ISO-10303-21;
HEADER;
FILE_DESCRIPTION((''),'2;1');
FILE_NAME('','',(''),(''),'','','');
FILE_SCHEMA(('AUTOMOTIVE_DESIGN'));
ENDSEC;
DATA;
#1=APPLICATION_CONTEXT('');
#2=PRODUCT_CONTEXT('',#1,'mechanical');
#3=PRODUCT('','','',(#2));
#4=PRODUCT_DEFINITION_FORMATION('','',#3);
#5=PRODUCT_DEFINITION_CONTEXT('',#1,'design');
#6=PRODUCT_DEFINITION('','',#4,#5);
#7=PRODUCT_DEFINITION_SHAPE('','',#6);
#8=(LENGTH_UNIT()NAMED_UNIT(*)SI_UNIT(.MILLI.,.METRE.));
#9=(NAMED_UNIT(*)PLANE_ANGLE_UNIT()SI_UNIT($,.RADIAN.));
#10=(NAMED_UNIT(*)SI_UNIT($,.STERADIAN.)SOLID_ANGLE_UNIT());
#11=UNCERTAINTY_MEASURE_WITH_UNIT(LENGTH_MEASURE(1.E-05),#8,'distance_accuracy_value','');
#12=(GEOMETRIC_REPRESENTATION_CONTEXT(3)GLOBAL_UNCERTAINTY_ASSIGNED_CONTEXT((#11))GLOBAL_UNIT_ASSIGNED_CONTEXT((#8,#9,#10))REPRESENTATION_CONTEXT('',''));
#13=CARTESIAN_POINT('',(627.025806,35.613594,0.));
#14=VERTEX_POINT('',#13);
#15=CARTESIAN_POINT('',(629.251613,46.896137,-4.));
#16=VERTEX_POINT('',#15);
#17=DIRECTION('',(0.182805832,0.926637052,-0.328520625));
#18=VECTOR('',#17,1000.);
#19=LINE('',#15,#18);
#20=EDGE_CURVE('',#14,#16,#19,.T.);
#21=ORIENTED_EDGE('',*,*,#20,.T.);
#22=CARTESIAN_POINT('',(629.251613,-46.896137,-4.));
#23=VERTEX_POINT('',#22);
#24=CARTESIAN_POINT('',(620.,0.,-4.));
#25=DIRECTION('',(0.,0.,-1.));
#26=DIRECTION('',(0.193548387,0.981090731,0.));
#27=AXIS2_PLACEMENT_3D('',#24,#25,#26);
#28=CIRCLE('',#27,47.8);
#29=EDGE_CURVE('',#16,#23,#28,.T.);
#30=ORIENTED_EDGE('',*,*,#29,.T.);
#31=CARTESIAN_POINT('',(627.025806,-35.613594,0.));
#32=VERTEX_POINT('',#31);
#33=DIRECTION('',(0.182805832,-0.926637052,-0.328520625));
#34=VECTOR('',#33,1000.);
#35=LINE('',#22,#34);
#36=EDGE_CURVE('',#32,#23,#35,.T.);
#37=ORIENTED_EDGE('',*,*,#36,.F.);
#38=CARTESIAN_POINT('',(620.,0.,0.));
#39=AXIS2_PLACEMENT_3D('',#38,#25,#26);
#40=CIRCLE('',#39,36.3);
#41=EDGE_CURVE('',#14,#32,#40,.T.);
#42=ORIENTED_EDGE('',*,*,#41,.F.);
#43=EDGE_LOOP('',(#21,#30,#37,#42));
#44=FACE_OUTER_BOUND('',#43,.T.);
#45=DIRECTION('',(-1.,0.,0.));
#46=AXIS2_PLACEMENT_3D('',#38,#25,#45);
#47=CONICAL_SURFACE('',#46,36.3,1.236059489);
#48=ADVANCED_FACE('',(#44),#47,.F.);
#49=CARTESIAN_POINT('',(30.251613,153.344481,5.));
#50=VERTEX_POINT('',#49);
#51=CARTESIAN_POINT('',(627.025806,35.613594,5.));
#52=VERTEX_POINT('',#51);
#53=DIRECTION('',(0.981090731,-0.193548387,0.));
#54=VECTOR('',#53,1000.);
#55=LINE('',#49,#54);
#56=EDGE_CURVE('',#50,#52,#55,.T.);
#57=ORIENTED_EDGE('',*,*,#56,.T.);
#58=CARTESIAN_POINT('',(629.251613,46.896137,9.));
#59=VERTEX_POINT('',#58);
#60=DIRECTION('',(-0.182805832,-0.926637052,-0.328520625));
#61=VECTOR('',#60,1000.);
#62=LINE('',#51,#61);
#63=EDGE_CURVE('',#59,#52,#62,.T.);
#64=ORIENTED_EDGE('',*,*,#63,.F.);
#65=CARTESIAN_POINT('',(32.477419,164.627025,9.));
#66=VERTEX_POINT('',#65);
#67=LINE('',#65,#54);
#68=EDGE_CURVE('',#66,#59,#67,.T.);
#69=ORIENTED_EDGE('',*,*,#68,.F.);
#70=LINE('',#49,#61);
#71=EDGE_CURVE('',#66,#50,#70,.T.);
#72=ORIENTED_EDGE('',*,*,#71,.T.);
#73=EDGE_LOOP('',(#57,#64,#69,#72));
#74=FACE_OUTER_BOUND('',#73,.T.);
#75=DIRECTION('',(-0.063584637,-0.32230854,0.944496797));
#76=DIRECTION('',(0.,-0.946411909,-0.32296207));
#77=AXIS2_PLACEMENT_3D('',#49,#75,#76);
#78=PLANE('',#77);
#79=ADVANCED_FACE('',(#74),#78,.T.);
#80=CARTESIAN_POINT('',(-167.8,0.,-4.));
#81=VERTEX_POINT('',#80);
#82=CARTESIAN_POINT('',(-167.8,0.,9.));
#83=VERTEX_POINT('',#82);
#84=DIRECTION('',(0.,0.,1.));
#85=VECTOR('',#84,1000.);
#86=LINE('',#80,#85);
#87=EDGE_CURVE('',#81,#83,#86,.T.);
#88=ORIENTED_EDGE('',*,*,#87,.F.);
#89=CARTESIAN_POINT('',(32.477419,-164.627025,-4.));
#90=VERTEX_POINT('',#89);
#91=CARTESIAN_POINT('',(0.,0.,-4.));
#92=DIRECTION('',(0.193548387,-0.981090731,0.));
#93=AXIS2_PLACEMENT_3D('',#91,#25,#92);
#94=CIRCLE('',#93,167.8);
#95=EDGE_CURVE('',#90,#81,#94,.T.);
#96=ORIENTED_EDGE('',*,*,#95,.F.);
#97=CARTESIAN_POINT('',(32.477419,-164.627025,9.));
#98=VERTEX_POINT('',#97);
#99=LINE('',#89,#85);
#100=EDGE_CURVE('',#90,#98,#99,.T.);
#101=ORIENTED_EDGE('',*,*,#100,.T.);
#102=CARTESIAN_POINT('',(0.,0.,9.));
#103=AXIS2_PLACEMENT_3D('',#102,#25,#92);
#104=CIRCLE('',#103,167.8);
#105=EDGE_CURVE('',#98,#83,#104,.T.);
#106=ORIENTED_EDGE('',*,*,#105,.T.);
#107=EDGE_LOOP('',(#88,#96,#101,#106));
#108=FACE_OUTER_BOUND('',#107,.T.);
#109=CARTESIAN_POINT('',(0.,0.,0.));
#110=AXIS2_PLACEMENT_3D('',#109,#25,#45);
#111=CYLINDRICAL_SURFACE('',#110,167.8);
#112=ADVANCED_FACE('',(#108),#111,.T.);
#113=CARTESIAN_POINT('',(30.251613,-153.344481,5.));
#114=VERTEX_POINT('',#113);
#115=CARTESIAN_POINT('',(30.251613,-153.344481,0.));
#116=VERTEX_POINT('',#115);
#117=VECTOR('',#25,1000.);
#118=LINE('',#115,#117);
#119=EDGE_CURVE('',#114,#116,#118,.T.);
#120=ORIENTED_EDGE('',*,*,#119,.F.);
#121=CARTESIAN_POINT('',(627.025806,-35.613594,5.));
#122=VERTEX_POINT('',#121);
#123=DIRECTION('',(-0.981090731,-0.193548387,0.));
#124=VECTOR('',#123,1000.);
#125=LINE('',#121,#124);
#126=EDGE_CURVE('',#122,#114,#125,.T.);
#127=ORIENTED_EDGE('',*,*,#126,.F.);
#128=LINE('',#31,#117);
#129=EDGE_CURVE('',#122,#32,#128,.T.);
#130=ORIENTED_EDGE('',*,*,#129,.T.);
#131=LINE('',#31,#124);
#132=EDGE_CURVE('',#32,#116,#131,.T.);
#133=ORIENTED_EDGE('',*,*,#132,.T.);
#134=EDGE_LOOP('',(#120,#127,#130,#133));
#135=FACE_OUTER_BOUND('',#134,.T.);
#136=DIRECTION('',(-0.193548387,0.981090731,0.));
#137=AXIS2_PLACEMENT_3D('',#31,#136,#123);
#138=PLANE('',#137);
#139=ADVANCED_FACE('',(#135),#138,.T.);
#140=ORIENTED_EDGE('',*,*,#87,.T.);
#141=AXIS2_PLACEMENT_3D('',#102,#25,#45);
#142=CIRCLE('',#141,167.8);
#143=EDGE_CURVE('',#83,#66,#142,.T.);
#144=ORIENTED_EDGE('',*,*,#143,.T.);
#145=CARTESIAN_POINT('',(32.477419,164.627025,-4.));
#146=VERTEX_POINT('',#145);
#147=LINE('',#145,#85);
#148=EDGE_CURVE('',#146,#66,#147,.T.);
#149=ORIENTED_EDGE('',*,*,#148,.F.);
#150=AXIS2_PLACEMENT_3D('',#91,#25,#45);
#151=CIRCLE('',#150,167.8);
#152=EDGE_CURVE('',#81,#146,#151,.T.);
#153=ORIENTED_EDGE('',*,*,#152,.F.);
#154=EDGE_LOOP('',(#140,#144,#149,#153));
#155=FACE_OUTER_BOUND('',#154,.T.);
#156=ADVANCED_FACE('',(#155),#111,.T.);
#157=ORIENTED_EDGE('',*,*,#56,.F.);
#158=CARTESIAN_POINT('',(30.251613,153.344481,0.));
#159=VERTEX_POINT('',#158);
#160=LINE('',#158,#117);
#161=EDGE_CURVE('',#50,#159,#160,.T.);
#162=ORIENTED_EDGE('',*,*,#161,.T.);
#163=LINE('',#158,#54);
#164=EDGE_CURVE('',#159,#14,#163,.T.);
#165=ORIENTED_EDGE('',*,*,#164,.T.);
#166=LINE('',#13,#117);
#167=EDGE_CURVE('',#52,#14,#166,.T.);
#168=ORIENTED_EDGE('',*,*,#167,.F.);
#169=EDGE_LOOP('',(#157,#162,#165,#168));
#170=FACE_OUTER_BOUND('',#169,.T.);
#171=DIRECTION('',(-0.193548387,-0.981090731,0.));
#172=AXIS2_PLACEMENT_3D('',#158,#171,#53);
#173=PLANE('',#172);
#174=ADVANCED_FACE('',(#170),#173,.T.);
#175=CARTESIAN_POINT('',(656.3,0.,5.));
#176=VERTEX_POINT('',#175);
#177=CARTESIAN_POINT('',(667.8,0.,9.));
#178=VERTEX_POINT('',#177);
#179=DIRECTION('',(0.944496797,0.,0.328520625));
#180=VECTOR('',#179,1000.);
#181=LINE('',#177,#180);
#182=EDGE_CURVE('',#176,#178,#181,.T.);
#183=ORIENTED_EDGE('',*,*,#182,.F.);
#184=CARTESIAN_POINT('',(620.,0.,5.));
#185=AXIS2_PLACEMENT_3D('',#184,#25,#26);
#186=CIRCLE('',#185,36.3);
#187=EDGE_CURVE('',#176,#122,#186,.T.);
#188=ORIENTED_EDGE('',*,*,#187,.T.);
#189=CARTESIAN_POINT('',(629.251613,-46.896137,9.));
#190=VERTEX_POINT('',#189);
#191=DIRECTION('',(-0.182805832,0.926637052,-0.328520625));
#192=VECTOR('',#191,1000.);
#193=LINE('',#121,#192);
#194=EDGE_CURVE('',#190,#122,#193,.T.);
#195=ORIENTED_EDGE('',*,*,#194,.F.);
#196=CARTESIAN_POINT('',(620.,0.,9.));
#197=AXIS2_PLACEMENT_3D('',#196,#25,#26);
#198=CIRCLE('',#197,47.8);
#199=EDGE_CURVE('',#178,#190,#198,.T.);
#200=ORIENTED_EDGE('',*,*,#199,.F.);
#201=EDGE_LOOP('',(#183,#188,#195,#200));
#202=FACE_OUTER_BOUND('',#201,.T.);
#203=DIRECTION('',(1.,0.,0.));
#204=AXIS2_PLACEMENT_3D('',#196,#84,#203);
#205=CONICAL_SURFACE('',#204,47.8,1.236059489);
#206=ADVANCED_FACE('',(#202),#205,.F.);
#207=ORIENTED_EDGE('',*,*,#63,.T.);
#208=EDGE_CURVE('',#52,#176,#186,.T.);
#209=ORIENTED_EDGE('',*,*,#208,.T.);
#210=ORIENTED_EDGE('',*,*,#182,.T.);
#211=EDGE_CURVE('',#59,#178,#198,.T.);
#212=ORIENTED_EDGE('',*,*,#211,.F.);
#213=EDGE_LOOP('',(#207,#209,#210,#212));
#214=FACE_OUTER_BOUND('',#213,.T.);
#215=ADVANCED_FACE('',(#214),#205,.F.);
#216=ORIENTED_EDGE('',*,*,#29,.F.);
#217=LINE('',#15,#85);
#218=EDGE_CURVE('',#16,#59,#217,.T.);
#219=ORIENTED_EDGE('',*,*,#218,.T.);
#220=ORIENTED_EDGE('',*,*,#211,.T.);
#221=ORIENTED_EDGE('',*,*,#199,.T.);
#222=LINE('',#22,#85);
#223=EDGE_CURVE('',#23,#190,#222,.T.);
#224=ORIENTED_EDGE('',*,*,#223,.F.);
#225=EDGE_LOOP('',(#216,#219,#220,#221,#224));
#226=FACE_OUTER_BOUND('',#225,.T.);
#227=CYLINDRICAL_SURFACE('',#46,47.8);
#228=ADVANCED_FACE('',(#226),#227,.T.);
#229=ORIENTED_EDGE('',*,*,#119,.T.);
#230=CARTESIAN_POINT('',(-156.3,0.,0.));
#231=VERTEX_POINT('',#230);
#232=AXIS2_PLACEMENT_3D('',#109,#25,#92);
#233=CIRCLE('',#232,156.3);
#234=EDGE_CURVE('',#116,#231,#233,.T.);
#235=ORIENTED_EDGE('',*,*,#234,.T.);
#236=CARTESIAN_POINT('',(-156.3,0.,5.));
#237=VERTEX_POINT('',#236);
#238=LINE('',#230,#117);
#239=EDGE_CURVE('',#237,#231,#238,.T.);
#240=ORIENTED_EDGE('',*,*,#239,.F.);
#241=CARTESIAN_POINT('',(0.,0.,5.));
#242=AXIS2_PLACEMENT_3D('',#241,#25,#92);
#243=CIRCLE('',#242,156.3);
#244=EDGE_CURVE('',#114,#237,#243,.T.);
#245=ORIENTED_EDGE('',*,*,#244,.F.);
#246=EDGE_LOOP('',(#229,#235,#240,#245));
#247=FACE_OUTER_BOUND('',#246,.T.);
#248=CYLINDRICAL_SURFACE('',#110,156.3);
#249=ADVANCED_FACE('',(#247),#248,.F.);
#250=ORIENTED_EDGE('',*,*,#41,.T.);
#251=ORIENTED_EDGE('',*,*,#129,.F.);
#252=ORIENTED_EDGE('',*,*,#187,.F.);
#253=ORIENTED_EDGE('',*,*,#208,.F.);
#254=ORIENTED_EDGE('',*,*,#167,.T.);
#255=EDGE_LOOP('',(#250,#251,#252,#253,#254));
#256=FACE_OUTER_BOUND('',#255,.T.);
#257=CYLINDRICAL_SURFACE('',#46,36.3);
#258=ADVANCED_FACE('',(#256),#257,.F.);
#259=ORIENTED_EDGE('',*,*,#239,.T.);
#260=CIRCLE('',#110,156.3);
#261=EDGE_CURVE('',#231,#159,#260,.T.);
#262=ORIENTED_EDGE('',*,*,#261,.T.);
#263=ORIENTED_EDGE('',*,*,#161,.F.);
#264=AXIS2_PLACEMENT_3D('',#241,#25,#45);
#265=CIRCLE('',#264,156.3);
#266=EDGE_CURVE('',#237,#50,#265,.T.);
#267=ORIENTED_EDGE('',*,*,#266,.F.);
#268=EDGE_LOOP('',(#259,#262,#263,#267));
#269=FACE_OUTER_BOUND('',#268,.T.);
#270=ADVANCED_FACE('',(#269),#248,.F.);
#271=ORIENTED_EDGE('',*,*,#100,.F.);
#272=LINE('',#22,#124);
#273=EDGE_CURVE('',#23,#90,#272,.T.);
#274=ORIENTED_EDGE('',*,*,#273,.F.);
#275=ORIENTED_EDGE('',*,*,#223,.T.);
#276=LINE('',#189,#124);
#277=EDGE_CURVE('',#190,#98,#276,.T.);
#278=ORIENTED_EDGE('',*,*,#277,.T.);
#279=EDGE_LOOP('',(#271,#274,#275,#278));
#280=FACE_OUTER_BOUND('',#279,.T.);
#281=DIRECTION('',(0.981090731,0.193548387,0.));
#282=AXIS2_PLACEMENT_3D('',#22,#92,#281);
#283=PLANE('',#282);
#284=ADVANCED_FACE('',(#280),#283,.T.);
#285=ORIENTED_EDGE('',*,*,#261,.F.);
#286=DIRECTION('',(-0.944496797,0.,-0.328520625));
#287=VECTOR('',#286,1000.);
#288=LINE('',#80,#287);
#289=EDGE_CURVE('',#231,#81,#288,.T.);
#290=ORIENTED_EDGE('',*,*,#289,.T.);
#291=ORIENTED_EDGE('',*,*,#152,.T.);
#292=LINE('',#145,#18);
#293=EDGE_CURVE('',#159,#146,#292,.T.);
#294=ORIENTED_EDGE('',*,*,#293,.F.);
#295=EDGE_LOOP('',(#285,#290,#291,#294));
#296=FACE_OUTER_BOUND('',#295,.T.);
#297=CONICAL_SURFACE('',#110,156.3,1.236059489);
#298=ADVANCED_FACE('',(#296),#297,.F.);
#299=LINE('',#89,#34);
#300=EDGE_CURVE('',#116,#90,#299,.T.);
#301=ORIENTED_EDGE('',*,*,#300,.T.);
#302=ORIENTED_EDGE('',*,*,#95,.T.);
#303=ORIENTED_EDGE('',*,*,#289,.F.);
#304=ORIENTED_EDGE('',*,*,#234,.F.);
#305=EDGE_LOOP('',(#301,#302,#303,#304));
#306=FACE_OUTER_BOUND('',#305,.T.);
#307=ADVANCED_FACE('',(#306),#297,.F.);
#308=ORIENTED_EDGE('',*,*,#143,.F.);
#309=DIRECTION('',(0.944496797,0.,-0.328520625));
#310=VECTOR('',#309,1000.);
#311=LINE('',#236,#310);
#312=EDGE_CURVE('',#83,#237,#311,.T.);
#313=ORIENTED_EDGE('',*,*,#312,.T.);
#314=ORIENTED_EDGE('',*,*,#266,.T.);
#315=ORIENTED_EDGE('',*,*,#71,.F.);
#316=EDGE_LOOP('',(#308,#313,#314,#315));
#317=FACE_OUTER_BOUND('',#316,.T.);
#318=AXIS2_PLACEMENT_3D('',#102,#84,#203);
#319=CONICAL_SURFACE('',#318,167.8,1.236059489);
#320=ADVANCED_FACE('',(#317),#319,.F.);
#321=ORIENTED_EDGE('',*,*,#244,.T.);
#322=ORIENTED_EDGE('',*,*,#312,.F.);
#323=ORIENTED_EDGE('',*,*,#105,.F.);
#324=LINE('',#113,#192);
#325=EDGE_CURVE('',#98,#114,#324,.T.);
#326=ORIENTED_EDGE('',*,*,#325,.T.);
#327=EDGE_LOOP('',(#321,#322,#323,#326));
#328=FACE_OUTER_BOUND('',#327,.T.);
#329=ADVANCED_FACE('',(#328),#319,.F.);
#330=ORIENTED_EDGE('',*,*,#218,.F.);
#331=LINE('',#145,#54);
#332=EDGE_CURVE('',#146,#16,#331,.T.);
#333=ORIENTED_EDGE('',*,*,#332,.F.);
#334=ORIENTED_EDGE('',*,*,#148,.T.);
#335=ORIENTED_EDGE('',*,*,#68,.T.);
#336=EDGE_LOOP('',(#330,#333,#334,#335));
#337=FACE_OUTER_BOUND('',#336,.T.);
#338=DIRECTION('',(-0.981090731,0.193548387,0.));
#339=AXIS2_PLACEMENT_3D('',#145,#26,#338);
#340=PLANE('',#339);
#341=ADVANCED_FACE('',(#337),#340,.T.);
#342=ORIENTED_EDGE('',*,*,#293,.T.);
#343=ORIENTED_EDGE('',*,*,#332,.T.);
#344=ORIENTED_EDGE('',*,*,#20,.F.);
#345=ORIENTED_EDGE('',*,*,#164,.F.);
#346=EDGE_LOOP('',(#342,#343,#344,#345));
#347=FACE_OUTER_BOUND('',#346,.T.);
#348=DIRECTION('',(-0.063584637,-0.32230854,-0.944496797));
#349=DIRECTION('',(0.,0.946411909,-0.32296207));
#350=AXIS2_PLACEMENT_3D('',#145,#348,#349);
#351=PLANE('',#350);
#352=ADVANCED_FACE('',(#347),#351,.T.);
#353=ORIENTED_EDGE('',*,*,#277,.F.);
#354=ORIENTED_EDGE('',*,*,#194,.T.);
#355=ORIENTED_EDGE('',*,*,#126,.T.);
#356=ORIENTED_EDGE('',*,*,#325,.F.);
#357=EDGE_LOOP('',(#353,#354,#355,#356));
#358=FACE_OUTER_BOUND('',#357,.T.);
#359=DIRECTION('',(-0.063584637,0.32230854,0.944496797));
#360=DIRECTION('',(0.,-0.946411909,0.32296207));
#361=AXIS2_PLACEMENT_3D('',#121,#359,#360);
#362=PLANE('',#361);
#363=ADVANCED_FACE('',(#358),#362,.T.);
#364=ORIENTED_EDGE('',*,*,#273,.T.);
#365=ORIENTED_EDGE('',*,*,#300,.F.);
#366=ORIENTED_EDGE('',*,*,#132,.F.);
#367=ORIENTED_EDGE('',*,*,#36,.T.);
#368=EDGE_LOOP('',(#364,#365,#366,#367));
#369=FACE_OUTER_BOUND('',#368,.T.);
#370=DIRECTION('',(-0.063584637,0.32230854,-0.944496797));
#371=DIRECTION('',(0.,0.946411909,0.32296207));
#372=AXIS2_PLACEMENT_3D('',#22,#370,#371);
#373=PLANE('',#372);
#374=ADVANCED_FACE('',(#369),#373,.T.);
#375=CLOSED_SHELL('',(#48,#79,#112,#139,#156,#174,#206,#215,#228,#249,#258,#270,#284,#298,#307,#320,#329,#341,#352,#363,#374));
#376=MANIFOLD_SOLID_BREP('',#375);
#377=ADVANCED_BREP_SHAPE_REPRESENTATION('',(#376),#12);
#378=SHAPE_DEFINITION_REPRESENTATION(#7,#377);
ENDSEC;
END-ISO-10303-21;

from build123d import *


with BuildPart() as part:
    # Sweep1: sweep along a path in Sketch1
    with BuildLine(Plane.XY) as sweep1_path:
        Line((30.251612903, 153.344481207), (627.025806452, 35.613593524))
        ThreePointArc((627.025806452, 35.613593524), (656.3, 0), (627.025806452, -35.613593524))
        Line((627.025806452, -35.613593524), (30.251612903, -153.344481207))
        ThreePointArc((30.251612903, -153.344481207), (-156.3, 0), (30.251612903, 153.344481207))
    # Sketch2 → Sweep1 (sweep)
    with BuildSketch(Plane(origin=(0, 0, 0), x_dir=(1, 0, 0), z_dir=(0, 1, 0))):
        Polygon((-156.3, 0), (-156.3, -5), (-167.8, -9), (-167.8, 4), align=None)
    sweep(path=sweep1_path.line)


solid = part.part
